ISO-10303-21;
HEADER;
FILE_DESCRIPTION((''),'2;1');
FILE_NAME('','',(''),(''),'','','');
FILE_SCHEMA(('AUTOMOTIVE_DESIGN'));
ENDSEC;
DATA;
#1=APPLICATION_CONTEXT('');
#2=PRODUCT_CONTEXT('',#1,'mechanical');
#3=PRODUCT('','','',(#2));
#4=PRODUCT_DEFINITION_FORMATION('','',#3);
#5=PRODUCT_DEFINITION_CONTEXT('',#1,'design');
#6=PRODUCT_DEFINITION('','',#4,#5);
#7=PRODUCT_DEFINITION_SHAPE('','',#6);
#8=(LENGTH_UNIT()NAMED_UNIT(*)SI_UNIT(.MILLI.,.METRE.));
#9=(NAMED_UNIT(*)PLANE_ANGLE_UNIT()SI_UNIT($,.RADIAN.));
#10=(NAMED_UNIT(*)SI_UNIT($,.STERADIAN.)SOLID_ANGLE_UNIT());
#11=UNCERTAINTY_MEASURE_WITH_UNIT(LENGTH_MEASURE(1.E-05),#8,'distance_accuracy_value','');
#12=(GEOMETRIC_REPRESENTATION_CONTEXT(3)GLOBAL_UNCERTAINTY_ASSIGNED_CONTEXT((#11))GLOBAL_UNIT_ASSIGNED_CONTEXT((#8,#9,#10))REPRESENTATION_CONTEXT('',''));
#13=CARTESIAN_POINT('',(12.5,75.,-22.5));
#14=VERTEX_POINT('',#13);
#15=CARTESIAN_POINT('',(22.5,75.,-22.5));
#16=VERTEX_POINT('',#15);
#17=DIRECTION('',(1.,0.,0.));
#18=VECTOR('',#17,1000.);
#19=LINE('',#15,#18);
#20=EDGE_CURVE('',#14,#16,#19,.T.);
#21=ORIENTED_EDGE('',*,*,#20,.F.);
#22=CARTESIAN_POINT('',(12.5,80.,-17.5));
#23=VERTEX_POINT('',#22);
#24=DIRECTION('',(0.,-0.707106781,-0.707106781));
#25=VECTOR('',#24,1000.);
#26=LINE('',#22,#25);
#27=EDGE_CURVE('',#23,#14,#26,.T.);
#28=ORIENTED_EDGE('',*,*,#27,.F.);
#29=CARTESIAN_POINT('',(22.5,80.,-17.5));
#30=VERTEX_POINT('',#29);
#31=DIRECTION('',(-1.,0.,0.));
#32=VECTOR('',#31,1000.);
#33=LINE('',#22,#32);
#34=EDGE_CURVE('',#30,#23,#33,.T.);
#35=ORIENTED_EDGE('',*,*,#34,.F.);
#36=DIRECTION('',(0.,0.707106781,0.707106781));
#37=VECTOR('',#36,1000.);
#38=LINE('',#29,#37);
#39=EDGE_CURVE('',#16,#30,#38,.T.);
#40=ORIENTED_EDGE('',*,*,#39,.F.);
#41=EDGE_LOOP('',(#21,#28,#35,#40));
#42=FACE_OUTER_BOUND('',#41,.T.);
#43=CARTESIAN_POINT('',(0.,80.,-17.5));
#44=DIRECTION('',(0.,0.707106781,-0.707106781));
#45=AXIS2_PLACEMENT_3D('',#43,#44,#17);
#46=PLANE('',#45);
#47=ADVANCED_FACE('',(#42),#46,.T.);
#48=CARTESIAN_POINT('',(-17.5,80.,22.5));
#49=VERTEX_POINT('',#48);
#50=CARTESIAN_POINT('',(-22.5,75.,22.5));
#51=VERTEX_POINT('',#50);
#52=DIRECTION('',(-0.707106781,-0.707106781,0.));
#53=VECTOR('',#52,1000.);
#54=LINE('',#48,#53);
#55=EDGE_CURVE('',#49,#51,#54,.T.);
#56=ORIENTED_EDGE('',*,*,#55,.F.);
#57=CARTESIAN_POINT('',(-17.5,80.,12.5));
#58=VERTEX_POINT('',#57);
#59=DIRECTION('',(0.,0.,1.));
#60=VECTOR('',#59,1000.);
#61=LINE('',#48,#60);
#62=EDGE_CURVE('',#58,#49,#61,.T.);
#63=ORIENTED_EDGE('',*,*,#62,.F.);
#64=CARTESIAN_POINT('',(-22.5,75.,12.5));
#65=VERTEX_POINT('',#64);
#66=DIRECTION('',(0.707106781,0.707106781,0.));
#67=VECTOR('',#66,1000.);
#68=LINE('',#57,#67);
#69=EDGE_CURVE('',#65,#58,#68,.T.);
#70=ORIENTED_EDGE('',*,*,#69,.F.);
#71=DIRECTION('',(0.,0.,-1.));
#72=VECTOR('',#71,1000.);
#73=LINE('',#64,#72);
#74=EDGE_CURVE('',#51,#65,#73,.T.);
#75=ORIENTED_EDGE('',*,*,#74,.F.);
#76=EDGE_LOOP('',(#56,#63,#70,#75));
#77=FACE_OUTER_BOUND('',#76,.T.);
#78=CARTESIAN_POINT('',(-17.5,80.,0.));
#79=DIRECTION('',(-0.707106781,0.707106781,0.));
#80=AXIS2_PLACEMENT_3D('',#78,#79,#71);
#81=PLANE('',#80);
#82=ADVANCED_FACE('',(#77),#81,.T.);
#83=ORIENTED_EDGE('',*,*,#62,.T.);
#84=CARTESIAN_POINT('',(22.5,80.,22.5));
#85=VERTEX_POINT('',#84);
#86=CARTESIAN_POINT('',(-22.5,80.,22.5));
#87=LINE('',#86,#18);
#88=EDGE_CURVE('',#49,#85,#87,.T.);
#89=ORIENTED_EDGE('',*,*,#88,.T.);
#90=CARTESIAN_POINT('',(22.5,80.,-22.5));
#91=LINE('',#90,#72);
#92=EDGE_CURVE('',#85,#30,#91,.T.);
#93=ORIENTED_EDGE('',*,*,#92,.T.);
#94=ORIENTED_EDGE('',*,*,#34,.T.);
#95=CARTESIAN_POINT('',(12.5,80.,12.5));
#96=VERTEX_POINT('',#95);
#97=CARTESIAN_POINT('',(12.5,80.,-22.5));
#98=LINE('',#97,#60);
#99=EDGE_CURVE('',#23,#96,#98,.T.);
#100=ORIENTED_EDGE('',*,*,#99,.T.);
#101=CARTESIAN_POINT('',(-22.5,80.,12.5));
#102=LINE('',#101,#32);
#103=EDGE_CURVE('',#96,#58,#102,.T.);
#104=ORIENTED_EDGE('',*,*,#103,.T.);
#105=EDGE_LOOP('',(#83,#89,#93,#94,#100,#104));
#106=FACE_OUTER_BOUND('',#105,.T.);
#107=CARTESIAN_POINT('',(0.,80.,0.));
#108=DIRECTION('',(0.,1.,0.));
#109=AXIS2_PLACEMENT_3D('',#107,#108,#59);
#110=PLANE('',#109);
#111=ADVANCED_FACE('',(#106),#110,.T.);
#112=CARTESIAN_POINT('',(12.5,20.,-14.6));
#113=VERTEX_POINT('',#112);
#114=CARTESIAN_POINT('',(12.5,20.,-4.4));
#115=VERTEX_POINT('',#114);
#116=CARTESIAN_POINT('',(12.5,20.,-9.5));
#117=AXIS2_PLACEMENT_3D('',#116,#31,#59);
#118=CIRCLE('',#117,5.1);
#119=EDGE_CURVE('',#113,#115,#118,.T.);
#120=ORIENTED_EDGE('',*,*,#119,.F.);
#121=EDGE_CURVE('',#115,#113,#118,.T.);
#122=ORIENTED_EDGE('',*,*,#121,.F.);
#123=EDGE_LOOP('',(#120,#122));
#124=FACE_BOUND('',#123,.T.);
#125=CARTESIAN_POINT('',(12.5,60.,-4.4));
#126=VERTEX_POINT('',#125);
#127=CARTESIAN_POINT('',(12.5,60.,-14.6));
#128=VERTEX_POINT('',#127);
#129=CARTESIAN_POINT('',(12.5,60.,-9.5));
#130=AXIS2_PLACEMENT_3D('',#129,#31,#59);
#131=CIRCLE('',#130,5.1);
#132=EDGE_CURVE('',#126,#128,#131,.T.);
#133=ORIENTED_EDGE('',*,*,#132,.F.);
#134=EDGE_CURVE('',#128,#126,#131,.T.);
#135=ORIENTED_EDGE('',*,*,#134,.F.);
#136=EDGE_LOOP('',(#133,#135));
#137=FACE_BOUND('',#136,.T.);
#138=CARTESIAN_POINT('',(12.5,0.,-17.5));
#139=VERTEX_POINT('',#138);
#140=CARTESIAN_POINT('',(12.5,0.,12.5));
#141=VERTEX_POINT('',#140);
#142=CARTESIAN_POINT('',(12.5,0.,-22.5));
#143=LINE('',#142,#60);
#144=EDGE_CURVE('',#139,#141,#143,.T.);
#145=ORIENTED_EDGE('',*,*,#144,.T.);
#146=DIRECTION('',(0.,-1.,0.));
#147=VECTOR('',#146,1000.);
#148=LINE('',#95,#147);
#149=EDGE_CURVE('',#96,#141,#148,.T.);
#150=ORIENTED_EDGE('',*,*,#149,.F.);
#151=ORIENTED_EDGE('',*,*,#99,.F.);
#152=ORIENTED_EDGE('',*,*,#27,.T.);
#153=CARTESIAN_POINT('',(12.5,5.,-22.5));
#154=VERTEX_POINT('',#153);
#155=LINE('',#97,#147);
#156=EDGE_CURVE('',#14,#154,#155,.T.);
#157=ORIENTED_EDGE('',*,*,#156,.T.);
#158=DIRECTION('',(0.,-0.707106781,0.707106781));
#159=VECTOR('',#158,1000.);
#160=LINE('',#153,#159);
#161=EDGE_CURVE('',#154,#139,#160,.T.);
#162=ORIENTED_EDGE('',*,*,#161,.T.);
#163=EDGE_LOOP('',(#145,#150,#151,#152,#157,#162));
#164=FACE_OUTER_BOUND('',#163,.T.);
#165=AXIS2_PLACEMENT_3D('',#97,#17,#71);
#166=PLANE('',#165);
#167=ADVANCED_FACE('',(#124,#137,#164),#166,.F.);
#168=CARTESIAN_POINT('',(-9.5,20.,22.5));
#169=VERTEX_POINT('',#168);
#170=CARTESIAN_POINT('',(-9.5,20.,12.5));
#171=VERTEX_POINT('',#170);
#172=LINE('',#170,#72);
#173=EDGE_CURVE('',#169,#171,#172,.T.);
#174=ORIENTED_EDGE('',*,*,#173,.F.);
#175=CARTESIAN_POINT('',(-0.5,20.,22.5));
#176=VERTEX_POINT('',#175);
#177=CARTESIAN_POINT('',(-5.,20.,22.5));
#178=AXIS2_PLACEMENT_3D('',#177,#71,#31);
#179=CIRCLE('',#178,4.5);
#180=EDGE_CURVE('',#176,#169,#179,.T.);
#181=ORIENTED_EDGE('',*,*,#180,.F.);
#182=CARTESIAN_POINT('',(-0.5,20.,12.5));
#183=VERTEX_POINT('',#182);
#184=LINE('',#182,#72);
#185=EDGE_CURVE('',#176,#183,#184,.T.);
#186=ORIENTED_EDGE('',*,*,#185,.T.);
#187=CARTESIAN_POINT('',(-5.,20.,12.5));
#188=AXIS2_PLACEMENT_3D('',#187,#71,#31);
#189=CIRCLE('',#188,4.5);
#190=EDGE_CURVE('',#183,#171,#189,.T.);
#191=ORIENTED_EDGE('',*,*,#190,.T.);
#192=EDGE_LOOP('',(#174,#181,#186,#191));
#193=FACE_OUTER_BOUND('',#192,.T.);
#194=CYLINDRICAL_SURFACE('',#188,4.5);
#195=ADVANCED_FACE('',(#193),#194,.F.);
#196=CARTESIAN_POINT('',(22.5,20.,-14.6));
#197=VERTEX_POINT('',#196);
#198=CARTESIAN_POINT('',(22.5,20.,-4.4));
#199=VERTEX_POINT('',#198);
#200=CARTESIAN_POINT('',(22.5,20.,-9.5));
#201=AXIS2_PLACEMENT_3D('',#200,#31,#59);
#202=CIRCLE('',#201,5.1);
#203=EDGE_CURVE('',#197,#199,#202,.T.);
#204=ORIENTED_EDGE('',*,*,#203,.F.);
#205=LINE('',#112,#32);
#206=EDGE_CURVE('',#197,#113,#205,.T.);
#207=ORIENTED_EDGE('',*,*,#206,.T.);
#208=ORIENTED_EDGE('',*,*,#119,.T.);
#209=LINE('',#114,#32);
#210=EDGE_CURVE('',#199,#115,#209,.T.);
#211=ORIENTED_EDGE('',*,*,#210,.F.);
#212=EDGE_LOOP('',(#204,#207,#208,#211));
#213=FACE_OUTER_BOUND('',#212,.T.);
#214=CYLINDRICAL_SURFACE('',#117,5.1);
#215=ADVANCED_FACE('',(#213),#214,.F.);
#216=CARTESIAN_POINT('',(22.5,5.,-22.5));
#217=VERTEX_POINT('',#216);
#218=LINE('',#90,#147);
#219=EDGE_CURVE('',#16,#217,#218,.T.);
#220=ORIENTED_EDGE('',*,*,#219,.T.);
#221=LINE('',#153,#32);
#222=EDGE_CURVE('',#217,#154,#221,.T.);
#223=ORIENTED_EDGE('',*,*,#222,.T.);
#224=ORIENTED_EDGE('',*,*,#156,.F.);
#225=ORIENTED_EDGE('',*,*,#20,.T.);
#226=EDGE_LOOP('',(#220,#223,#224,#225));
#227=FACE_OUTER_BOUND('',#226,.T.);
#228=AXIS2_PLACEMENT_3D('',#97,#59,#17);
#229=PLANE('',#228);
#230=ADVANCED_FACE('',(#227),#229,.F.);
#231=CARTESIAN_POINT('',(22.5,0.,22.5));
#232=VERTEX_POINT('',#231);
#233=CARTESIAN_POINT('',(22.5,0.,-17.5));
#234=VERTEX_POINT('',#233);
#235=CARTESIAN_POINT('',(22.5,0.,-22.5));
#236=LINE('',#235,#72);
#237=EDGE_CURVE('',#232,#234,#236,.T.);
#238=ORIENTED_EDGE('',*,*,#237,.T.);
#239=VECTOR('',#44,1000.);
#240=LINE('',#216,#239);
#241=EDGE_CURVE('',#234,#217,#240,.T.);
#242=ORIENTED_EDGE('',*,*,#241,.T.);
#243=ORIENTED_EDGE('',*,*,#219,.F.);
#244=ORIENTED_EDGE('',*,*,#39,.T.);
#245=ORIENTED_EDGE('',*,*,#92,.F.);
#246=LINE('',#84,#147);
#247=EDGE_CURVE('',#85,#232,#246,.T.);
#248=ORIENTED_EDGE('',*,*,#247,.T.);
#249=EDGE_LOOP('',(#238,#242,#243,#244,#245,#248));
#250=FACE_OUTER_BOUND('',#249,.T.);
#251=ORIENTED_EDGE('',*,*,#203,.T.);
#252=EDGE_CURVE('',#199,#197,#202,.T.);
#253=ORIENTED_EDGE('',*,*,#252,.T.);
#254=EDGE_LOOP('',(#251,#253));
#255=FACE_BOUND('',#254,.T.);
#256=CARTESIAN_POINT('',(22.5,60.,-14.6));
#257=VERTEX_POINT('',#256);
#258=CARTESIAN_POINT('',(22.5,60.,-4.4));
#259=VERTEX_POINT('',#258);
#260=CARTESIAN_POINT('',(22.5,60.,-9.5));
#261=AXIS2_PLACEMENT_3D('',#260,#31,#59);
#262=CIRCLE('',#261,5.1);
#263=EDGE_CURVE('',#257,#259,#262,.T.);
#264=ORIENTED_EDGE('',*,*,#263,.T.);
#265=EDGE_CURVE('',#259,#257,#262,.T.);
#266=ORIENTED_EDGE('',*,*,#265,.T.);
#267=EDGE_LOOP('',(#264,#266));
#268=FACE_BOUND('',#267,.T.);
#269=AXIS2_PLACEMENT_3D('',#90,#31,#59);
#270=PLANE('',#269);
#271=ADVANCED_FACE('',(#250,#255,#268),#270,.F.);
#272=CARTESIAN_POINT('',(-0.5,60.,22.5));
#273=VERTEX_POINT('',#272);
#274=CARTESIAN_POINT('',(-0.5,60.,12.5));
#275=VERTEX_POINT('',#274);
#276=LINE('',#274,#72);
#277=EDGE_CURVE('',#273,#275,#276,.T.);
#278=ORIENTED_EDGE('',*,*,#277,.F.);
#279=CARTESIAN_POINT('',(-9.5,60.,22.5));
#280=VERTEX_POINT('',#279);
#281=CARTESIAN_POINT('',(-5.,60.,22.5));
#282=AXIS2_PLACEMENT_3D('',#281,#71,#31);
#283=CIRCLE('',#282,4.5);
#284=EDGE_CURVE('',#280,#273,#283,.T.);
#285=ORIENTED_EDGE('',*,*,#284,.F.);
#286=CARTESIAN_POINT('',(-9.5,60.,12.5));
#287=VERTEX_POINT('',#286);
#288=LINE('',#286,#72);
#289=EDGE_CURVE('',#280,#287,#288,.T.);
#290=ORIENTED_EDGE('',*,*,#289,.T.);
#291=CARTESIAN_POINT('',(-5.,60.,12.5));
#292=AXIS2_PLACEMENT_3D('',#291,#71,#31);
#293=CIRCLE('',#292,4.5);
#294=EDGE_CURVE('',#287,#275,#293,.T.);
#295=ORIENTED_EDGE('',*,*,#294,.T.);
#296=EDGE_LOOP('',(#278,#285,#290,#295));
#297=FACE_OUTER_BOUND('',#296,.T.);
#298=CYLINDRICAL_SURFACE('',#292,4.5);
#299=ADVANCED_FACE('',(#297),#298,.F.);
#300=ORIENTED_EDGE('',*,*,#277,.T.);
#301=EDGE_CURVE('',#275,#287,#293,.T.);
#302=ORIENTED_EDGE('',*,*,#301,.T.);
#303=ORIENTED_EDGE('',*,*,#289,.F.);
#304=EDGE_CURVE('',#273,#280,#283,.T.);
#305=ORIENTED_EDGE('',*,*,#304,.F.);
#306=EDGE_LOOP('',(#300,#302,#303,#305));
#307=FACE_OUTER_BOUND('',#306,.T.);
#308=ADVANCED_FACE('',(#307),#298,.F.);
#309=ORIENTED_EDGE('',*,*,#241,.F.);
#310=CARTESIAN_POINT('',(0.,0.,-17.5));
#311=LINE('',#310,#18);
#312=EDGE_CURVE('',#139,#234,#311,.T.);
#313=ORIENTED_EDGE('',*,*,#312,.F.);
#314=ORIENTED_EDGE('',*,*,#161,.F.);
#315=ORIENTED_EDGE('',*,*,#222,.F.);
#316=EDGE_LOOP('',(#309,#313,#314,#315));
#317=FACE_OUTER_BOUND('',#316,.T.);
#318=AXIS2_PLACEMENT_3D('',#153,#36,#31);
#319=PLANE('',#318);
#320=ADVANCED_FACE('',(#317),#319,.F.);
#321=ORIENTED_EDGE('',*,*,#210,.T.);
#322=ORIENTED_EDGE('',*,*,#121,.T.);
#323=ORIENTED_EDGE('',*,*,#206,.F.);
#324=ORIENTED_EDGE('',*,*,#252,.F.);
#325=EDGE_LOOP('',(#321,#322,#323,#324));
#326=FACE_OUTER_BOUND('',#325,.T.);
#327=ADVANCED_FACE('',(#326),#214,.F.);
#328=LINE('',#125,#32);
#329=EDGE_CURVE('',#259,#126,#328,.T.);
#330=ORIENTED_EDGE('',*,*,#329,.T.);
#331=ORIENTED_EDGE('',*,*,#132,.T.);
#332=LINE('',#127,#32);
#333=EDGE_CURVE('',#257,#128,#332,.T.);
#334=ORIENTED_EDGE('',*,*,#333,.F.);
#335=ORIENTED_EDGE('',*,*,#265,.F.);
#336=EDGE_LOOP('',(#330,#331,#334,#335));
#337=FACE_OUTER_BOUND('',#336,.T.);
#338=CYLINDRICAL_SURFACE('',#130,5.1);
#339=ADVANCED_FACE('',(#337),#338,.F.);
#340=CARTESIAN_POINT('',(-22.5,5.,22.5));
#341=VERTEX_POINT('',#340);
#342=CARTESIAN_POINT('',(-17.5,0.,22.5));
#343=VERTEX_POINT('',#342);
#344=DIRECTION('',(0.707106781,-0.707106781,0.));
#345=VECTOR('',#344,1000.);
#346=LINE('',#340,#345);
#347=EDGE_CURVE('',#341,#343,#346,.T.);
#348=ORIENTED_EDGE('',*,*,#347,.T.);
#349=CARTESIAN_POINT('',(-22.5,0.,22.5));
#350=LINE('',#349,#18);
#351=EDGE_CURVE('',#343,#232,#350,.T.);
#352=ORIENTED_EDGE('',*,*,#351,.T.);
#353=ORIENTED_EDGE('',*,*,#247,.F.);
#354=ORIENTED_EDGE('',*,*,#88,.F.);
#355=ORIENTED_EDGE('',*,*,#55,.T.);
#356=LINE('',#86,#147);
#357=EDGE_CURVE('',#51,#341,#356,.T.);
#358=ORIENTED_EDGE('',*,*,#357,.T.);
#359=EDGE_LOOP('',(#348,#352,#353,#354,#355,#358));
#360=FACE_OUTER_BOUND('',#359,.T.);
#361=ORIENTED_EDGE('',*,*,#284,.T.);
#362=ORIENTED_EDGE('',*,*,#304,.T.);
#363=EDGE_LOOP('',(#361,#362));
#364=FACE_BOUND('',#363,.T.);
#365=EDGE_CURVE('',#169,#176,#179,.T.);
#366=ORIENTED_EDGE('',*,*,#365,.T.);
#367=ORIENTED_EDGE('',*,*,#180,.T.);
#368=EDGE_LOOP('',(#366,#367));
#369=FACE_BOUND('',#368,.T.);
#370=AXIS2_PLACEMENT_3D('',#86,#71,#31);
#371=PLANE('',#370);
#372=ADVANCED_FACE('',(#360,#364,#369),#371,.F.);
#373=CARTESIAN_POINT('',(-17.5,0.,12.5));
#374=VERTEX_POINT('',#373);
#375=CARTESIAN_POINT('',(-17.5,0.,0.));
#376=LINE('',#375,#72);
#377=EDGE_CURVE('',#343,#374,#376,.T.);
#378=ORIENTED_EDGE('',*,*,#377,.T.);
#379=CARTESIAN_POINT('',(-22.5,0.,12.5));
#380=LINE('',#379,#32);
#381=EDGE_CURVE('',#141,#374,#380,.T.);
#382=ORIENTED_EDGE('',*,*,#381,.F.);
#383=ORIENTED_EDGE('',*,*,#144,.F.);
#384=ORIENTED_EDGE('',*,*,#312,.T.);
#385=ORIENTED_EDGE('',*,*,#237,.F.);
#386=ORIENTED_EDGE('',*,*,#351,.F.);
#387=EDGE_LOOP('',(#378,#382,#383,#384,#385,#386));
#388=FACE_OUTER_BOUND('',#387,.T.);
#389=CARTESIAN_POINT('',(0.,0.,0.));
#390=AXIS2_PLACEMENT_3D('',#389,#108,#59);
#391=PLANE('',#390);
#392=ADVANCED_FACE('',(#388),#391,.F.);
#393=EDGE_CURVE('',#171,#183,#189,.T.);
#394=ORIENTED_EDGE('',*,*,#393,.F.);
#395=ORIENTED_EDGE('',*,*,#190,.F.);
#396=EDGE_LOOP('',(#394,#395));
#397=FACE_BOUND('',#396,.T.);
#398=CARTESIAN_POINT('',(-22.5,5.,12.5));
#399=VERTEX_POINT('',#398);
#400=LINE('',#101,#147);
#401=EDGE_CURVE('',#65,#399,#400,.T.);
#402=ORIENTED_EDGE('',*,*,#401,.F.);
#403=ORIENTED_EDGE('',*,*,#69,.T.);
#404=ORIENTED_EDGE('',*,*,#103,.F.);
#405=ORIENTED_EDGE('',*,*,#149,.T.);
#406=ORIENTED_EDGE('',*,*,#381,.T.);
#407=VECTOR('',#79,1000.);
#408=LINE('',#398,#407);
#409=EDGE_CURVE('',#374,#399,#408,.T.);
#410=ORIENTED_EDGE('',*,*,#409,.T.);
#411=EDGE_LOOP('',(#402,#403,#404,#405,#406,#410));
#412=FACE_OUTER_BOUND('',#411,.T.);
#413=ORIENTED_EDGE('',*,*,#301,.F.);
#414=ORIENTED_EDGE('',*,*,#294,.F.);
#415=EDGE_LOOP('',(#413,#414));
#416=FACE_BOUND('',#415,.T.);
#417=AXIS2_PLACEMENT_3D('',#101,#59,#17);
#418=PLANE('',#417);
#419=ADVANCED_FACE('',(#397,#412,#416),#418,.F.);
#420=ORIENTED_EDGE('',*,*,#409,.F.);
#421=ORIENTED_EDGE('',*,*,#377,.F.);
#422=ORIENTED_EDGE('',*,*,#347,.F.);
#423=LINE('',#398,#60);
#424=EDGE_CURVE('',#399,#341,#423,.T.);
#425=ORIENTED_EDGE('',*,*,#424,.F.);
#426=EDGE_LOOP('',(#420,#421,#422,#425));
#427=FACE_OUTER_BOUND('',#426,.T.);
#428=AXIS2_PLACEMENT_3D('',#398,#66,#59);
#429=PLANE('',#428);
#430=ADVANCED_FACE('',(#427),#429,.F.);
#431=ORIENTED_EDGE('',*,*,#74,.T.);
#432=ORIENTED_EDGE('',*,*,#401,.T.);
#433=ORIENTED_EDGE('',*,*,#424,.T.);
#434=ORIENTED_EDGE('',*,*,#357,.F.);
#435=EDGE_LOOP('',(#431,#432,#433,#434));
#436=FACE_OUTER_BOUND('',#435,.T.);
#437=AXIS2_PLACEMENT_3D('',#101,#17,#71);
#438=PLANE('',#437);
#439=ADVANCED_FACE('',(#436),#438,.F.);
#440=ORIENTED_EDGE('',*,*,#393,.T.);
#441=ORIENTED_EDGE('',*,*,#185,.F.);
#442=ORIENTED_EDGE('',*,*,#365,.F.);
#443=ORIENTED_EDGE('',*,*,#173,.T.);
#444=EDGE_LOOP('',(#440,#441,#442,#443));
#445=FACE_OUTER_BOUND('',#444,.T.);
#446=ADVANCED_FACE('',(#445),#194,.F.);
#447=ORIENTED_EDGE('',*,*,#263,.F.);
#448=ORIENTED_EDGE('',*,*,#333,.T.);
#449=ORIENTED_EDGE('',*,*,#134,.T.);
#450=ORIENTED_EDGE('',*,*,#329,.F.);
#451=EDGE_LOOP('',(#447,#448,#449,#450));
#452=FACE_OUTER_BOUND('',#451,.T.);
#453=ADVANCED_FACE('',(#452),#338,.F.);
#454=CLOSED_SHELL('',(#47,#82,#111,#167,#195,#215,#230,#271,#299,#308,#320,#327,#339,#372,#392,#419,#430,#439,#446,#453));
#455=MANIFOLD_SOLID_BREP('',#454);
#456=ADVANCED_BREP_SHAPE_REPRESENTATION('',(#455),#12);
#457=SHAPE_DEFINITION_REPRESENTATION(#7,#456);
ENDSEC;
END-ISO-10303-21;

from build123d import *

# Parameters (mm, degrees)
EXTRUDE_1_DEPTH        = 80
CHAMFER_1_SIZE         = 5
HOLE_WIZARD_M8_1_D     = 9
HOLE_WIZARD_M8_1_DEPTH = 15
HOLE_WIZARD_M8_1_TIP   = 2.703872786
HOLE_WIZARD_M12_1_D    = 10.2
PATTERN_LINEAR_1_COUNT = 2
PATTERN_LINEAR_1_PITCH = 40


with BuildPart() as part:
    # 草图1 → 凸台-拉伸1 (new body)
    with BuildSketch(Plane(origin=(0, 0, 0), x_dir=(1, 0, 0), z_dir=(0, 1, 0))):
        Polygon((-22.5, -12.5), (12.5, -12.5), (12.5, 22.5), (22.5, 22.5), (22.5, -22.5), (-22.5, -22.5), align=None)
    extrude(amount=EXTRUDE_1_DEPTH)

    # 倒角1
    chamfer_1_edges = [part.edges().sort_by_distance(p)[0] for p in [
        (-22.5, 80, 17.5),
        (-22.5, 0, 17.5),
        (17.5, 80, -22.5),
        (17.5, 0, -22.5),
    ]]
    chamfer(chamfer_1_edges, length=CHAMFER_1_SIZE)

    # M8 间隙孔1
    with Locations(Plane(origin=(-5, 60, 12.5), x_dir=(-1, 0, 0), z_dir=(0, 0, -1))):
        with Locations((0, 0), (0, -40)):
            Hole(HOLE_WIZARD_M8_1_D / 2, depth=HOLE_WIZARD_M8_1_DEPTH)
            with Locations((0, 0, -(HOLE_WIZARD_M8_1_DEPTH + HOLE_WIZARD_M8_1_TIP / 2))):  # 118° drill point
                Cone(0, HOLE_WIZARD_M8_1_D / 2, HOLE_WIZARD_M8_1_TIP, mode=Mode.SUBTRACT)

    # M12 螺纹孔1 (through all)
    with Locations(Plane(origin=(12.5, 60, -9.5), x_dir=(0, 0, -1), z_dir=(-1, 0, 0))):
        with Locations((0, 0)):
            hole_wizard_m12_1 = Hole(HOLE_WIZARD_M12_1_D / 2)

    # 阵列(线性)1: M12 螺纹孔1 ×2
    with Locations(*[(0, -i * PATTERN_LINEAR_1_PITCH, 0) for i in range(1, PATTERN_LINEAR_1_COUNT)]):
        add(hole_wizard_m12_1, mode=Mode.SUBTRACT)


solid = part.part
